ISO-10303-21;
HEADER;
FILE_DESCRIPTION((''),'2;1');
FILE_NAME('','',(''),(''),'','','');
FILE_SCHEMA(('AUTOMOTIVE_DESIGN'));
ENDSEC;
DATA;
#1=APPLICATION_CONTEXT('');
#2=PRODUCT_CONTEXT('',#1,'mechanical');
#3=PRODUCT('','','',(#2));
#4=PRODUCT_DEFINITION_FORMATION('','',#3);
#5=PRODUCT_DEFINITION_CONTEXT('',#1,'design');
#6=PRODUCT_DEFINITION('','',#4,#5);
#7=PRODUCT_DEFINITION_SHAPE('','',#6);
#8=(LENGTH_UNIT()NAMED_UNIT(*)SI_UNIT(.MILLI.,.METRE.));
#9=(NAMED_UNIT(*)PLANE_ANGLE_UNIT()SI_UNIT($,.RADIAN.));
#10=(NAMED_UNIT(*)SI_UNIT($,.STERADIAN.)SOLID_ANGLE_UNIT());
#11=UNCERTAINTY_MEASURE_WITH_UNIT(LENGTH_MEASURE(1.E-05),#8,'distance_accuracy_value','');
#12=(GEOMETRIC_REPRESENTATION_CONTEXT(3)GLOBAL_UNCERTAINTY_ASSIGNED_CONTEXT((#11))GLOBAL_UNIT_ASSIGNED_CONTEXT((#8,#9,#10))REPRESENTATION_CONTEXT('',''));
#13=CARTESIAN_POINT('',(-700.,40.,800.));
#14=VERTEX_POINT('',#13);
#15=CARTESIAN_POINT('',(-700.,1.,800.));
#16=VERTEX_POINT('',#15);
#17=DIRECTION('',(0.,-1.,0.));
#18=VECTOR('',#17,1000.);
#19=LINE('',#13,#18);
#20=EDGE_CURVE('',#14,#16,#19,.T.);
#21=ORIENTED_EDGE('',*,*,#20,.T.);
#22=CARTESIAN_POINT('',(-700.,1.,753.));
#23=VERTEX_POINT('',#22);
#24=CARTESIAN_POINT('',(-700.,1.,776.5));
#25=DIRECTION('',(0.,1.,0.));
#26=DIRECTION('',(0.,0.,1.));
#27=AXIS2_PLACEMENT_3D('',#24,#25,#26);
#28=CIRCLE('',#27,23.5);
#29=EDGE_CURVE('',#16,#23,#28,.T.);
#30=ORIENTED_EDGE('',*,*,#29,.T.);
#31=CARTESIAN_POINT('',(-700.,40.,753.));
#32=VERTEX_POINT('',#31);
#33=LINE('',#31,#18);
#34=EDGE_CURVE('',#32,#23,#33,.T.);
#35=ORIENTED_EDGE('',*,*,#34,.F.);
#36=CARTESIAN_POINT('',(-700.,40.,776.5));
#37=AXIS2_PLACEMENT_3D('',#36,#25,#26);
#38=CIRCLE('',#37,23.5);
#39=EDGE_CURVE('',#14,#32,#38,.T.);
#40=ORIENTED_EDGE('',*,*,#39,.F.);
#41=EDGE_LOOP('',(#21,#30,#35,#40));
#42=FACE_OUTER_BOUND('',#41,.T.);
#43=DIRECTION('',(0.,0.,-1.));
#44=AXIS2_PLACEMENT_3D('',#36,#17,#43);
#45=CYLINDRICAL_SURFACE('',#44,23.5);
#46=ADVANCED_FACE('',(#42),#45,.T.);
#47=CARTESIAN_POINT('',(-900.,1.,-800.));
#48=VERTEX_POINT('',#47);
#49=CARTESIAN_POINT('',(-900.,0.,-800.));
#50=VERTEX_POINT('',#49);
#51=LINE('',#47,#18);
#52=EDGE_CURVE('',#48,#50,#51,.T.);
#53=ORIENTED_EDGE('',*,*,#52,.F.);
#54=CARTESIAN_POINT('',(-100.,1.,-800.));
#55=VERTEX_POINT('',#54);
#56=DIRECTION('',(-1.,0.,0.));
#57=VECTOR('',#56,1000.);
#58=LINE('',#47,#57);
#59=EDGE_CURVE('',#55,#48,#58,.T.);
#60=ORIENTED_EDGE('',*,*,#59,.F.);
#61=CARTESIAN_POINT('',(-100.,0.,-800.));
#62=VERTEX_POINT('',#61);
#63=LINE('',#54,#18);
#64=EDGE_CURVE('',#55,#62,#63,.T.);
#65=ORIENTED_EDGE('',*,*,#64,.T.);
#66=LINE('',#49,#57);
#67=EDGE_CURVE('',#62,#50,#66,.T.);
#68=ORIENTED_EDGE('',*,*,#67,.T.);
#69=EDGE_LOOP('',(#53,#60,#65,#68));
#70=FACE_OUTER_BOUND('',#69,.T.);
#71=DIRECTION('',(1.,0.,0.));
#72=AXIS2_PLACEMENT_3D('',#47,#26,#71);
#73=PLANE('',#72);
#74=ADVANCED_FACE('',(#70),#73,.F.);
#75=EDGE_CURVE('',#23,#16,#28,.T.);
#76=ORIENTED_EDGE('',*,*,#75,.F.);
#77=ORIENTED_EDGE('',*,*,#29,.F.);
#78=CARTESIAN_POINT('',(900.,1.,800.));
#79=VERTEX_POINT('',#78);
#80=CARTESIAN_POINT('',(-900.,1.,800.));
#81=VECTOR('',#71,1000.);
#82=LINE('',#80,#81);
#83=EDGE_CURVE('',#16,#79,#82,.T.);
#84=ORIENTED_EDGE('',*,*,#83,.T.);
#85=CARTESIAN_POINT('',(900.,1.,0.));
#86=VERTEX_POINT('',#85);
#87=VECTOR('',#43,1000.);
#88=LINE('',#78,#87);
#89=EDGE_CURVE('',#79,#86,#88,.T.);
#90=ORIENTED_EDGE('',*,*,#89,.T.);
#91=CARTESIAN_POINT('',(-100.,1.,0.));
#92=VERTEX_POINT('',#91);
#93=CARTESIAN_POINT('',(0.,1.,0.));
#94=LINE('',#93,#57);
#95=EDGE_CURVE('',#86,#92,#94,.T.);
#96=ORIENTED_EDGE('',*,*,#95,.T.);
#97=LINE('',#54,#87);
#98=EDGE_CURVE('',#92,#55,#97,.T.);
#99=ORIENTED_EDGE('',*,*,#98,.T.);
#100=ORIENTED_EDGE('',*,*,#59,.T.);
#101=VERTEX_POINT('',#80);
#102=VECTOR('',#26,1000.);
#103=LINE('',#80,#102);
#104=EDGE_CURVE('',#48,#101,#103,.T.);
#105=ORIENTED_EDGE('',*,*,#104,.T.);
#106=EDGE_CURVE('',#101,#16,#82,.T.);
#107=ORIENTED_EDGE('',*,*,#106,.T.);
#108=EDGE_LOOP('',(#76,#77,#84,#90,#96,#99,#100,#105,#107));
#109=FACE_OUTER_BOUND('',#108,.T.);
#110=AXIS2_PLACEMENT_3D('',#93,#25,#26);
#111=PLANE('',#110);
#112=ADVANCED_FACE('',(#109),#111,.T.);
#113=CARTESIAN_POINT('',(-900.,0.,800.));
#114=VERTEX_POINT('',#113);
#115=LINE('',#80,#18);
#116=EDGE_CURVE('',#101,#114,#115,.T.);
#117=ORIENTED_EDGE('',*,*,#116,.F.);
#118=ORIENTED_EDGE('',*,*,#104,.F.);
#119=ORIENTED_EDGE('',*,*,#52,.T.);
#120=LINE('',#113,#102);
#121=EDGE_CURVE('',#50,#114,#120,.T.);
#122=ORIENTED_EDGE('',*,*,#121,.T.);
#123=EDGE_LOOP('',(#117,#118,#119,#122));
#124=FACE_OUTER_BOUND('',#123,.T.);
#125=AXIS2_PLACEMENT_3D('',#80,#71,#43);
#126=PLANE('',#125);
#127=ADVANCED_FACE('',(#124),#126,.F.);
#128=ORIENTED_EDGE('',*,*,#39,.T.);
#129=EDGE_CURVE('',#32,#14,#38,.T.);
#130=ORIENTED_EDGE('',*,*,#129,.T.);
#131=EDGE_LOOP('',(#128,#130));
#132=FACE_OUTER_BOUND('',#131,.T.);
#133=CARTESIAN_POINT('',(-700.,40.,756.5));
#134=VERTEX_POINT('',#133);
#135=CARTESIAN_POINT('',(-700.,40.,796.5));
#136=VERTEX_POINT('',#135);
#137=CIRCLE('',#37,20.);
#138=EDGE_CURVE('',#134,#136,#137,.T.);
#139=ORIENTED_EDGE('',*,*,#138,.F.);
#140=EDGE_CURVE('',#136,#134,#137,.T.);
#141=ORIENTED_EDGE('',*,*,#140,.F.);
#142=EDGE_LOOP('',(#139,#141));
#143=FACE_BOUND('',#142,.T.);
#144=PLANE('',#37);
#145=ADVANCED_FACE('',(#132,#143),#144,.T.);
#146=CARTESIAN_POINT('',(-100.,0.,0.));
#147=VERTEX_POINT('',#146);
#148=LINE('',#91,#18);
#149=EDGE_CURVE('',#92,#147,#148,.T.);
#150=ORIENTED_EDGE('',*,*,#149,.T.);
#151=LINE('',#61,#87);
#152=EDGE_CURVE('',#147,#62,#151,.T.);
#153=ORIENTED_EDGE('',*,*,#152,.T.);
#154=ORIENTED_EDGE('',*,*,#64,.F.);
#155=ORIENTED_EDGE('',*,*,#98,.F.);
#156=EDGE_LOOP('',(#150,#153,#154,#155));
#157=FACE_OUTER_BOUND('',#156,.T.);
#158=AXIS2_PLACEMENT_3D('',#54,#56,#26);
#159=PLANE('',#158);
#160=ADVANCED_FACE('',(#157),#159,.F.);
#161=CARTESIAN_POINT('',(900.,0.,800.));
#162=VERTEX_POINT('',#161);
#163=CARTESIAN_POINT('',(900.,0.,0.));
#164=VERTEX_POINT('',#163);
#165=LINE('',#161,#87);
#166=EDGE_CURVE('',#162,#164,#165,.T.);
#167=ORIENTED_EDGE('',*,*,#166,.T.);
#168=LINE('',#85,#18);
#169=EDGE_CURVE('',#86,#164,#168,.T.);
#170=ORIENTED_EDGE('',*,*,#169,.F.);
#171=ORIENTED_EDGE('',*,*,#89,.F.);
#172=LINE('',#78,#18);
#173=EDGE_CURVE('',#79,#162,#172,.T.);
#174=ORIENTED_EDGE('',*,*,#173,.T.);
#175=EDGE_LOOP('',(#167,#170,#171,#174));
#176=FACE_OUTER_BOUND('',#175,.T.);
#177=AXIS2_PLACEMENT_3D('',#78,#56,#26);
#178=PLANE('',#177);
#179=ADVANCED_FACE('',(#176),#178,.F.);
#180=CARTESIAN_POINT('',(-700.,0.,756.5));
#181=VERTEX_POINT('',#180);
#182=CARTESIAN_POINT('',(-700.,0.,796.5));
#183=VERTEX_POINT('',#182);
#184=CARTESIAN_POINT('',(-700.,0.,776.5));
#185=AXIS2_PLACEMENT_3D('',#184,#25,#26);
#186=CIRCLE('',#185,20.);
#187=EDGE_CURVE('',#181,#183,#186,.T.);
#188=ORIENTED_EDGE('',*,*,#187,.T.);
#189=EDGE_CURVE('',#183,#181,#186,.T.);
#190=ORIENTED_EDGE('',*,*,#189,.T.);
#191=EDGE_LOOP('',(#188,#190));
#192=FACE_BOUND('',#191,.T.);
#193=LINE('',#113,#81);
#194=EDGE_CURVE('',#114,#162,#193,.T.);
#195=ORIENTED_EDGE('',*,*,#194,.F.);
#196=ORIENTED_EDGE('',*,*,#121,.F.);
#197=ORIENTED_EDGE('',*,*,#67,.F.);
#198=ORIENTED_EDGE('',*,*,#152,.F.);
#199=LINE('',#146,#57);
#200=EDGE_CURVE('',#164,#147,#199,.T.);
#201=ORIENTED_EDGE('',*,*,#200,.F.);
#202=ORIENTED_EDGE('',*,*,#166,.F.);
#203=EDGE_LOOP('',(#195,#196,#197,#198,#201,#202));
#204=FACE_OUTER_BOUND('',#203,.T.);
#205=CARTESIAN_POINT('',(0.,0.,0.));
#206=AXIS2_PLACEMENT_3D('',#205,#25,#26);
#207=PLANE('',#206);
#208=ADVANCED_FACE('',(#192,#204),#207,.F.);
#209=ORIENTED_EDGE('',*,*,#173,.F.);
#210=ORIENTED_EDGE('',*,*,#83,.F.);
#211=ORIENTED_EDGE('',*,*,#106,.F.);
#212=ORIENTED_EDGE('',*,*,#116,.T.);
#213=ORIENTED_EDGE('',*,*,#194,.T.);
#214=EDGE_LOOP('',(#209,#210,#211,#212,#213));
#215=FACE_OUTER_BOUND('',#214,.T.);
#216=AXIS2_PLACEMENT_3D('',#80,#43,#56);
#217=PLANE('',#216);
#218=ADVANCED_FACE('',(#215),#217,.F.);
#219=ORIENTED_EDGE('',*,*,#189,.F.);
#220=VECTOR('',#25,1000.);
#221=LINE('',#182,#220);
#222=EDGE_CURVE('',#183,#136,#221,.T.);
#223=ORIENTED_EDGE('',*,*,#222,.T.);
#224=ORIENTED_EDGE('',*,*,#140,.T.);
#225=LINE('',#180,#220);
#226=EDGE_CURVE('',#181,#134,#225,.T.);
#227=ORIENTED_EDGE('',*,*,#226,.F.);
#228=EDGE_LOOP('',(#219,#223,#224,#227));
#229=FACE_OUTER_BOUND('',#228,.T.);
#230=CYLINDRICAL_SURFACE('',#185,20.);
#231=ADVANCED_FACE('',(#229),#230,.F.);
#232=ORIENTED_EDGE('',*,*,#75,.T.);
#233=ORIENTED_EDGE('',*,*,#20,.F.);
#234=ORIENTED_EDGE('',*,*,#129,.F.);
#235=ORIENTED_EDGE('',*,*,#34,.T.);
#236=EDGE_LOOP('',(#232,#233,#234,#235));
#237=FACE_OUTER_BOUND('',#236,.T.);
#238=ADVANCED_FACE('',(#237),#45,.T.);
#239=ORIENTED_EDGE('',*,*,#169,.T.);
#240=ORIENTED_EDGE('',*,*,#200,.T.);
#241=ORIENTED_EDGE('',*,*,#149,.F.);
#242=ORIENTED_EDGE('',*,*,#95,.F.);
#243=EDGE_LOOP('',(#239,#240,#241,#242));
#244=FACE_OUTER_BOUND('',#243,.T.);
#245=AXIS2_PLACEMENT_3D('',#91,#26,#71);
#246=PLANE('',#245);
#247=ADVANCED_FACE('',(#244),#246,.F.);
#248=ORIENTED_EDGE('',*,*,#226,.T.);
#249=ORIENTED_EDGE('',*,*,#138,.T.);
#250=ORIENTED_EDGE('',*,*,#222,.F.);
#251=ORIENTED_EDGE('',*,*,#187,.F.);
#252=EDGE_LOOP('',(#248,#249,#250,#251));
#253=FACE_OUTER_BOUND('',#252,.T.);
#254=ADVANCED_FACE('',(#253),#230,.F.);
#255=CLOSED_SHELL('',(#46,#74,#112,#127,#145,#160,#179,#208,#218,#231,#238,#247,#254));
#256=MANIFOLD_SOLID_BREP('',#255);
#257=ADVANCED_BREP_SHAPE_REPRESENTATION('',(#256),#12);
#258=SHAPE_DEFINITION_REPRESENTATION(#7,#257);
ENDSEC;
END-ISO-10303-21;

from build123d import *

# Parameters (mm, degrees)
BOSS_EXTRUDE1_DEPTH = 1
SKETCH2_R           = 20
CUT_EXTRUDE1_DEPTH  = 1205.159873107
BOSS_EXTRUDE2_START = 39
SKETCH3_R           = 23.5
SKETCH3_R_2         = 20
BOSS_EXTRUDE2_DEPTH = 39


with BuildPart() as part:
    # Sketch1 → Boss-Extrude1 (new body)
    with BuildSketch(Plane(origin=(0, 0, 0), x_dir=(1, 0, 0), z_dir=(0, 1, 0))):
        Polygon((-900, -800), (900, -800), (900, 0), (0, 0), (-100, 0), (-100, 800), (-900, 800), align=None)
    extrude(amount=BOSS_EXTRUDE1_DEPTH)

    # Sketch2 → Cut-Extrude1 (cut, through all)
    with BuildSketch(Plane(origin=(0, 1, 0), x_dir=(1, 0, 0), z_dir=(0, 1, 0))):
        with Locations(Location((-700, -776.5, 0), (0, 0, 270))):
            Circle(SKETCH2_R)
    extrude(amount=-CUT_EXTRUDE1_DEPTH, mode=Mode.SUBTRACT)

    # Sketch3 → Boss-Extrude2 (add)
    with BuildSketch(Plane(origin=(0, 1, 0), x_dir=(1, 0, 0), z_dir=(0, 1, 0)).offset(BOSS_EXTRUDE2_START)):
        with Locations(Location((-700, -776.5, 0), (0, 0, 270))):
            Circle(SKETCH3_R)
        with Locations(Location((-700, -776.5, 0), (0, 0, 270))):
            Circle(SKETCH3_R_2, mode=Mode.SUBTRACT)
    extrude(amount=-BOSS_EXTRUDE2_DEPTH)


solid = part.part
